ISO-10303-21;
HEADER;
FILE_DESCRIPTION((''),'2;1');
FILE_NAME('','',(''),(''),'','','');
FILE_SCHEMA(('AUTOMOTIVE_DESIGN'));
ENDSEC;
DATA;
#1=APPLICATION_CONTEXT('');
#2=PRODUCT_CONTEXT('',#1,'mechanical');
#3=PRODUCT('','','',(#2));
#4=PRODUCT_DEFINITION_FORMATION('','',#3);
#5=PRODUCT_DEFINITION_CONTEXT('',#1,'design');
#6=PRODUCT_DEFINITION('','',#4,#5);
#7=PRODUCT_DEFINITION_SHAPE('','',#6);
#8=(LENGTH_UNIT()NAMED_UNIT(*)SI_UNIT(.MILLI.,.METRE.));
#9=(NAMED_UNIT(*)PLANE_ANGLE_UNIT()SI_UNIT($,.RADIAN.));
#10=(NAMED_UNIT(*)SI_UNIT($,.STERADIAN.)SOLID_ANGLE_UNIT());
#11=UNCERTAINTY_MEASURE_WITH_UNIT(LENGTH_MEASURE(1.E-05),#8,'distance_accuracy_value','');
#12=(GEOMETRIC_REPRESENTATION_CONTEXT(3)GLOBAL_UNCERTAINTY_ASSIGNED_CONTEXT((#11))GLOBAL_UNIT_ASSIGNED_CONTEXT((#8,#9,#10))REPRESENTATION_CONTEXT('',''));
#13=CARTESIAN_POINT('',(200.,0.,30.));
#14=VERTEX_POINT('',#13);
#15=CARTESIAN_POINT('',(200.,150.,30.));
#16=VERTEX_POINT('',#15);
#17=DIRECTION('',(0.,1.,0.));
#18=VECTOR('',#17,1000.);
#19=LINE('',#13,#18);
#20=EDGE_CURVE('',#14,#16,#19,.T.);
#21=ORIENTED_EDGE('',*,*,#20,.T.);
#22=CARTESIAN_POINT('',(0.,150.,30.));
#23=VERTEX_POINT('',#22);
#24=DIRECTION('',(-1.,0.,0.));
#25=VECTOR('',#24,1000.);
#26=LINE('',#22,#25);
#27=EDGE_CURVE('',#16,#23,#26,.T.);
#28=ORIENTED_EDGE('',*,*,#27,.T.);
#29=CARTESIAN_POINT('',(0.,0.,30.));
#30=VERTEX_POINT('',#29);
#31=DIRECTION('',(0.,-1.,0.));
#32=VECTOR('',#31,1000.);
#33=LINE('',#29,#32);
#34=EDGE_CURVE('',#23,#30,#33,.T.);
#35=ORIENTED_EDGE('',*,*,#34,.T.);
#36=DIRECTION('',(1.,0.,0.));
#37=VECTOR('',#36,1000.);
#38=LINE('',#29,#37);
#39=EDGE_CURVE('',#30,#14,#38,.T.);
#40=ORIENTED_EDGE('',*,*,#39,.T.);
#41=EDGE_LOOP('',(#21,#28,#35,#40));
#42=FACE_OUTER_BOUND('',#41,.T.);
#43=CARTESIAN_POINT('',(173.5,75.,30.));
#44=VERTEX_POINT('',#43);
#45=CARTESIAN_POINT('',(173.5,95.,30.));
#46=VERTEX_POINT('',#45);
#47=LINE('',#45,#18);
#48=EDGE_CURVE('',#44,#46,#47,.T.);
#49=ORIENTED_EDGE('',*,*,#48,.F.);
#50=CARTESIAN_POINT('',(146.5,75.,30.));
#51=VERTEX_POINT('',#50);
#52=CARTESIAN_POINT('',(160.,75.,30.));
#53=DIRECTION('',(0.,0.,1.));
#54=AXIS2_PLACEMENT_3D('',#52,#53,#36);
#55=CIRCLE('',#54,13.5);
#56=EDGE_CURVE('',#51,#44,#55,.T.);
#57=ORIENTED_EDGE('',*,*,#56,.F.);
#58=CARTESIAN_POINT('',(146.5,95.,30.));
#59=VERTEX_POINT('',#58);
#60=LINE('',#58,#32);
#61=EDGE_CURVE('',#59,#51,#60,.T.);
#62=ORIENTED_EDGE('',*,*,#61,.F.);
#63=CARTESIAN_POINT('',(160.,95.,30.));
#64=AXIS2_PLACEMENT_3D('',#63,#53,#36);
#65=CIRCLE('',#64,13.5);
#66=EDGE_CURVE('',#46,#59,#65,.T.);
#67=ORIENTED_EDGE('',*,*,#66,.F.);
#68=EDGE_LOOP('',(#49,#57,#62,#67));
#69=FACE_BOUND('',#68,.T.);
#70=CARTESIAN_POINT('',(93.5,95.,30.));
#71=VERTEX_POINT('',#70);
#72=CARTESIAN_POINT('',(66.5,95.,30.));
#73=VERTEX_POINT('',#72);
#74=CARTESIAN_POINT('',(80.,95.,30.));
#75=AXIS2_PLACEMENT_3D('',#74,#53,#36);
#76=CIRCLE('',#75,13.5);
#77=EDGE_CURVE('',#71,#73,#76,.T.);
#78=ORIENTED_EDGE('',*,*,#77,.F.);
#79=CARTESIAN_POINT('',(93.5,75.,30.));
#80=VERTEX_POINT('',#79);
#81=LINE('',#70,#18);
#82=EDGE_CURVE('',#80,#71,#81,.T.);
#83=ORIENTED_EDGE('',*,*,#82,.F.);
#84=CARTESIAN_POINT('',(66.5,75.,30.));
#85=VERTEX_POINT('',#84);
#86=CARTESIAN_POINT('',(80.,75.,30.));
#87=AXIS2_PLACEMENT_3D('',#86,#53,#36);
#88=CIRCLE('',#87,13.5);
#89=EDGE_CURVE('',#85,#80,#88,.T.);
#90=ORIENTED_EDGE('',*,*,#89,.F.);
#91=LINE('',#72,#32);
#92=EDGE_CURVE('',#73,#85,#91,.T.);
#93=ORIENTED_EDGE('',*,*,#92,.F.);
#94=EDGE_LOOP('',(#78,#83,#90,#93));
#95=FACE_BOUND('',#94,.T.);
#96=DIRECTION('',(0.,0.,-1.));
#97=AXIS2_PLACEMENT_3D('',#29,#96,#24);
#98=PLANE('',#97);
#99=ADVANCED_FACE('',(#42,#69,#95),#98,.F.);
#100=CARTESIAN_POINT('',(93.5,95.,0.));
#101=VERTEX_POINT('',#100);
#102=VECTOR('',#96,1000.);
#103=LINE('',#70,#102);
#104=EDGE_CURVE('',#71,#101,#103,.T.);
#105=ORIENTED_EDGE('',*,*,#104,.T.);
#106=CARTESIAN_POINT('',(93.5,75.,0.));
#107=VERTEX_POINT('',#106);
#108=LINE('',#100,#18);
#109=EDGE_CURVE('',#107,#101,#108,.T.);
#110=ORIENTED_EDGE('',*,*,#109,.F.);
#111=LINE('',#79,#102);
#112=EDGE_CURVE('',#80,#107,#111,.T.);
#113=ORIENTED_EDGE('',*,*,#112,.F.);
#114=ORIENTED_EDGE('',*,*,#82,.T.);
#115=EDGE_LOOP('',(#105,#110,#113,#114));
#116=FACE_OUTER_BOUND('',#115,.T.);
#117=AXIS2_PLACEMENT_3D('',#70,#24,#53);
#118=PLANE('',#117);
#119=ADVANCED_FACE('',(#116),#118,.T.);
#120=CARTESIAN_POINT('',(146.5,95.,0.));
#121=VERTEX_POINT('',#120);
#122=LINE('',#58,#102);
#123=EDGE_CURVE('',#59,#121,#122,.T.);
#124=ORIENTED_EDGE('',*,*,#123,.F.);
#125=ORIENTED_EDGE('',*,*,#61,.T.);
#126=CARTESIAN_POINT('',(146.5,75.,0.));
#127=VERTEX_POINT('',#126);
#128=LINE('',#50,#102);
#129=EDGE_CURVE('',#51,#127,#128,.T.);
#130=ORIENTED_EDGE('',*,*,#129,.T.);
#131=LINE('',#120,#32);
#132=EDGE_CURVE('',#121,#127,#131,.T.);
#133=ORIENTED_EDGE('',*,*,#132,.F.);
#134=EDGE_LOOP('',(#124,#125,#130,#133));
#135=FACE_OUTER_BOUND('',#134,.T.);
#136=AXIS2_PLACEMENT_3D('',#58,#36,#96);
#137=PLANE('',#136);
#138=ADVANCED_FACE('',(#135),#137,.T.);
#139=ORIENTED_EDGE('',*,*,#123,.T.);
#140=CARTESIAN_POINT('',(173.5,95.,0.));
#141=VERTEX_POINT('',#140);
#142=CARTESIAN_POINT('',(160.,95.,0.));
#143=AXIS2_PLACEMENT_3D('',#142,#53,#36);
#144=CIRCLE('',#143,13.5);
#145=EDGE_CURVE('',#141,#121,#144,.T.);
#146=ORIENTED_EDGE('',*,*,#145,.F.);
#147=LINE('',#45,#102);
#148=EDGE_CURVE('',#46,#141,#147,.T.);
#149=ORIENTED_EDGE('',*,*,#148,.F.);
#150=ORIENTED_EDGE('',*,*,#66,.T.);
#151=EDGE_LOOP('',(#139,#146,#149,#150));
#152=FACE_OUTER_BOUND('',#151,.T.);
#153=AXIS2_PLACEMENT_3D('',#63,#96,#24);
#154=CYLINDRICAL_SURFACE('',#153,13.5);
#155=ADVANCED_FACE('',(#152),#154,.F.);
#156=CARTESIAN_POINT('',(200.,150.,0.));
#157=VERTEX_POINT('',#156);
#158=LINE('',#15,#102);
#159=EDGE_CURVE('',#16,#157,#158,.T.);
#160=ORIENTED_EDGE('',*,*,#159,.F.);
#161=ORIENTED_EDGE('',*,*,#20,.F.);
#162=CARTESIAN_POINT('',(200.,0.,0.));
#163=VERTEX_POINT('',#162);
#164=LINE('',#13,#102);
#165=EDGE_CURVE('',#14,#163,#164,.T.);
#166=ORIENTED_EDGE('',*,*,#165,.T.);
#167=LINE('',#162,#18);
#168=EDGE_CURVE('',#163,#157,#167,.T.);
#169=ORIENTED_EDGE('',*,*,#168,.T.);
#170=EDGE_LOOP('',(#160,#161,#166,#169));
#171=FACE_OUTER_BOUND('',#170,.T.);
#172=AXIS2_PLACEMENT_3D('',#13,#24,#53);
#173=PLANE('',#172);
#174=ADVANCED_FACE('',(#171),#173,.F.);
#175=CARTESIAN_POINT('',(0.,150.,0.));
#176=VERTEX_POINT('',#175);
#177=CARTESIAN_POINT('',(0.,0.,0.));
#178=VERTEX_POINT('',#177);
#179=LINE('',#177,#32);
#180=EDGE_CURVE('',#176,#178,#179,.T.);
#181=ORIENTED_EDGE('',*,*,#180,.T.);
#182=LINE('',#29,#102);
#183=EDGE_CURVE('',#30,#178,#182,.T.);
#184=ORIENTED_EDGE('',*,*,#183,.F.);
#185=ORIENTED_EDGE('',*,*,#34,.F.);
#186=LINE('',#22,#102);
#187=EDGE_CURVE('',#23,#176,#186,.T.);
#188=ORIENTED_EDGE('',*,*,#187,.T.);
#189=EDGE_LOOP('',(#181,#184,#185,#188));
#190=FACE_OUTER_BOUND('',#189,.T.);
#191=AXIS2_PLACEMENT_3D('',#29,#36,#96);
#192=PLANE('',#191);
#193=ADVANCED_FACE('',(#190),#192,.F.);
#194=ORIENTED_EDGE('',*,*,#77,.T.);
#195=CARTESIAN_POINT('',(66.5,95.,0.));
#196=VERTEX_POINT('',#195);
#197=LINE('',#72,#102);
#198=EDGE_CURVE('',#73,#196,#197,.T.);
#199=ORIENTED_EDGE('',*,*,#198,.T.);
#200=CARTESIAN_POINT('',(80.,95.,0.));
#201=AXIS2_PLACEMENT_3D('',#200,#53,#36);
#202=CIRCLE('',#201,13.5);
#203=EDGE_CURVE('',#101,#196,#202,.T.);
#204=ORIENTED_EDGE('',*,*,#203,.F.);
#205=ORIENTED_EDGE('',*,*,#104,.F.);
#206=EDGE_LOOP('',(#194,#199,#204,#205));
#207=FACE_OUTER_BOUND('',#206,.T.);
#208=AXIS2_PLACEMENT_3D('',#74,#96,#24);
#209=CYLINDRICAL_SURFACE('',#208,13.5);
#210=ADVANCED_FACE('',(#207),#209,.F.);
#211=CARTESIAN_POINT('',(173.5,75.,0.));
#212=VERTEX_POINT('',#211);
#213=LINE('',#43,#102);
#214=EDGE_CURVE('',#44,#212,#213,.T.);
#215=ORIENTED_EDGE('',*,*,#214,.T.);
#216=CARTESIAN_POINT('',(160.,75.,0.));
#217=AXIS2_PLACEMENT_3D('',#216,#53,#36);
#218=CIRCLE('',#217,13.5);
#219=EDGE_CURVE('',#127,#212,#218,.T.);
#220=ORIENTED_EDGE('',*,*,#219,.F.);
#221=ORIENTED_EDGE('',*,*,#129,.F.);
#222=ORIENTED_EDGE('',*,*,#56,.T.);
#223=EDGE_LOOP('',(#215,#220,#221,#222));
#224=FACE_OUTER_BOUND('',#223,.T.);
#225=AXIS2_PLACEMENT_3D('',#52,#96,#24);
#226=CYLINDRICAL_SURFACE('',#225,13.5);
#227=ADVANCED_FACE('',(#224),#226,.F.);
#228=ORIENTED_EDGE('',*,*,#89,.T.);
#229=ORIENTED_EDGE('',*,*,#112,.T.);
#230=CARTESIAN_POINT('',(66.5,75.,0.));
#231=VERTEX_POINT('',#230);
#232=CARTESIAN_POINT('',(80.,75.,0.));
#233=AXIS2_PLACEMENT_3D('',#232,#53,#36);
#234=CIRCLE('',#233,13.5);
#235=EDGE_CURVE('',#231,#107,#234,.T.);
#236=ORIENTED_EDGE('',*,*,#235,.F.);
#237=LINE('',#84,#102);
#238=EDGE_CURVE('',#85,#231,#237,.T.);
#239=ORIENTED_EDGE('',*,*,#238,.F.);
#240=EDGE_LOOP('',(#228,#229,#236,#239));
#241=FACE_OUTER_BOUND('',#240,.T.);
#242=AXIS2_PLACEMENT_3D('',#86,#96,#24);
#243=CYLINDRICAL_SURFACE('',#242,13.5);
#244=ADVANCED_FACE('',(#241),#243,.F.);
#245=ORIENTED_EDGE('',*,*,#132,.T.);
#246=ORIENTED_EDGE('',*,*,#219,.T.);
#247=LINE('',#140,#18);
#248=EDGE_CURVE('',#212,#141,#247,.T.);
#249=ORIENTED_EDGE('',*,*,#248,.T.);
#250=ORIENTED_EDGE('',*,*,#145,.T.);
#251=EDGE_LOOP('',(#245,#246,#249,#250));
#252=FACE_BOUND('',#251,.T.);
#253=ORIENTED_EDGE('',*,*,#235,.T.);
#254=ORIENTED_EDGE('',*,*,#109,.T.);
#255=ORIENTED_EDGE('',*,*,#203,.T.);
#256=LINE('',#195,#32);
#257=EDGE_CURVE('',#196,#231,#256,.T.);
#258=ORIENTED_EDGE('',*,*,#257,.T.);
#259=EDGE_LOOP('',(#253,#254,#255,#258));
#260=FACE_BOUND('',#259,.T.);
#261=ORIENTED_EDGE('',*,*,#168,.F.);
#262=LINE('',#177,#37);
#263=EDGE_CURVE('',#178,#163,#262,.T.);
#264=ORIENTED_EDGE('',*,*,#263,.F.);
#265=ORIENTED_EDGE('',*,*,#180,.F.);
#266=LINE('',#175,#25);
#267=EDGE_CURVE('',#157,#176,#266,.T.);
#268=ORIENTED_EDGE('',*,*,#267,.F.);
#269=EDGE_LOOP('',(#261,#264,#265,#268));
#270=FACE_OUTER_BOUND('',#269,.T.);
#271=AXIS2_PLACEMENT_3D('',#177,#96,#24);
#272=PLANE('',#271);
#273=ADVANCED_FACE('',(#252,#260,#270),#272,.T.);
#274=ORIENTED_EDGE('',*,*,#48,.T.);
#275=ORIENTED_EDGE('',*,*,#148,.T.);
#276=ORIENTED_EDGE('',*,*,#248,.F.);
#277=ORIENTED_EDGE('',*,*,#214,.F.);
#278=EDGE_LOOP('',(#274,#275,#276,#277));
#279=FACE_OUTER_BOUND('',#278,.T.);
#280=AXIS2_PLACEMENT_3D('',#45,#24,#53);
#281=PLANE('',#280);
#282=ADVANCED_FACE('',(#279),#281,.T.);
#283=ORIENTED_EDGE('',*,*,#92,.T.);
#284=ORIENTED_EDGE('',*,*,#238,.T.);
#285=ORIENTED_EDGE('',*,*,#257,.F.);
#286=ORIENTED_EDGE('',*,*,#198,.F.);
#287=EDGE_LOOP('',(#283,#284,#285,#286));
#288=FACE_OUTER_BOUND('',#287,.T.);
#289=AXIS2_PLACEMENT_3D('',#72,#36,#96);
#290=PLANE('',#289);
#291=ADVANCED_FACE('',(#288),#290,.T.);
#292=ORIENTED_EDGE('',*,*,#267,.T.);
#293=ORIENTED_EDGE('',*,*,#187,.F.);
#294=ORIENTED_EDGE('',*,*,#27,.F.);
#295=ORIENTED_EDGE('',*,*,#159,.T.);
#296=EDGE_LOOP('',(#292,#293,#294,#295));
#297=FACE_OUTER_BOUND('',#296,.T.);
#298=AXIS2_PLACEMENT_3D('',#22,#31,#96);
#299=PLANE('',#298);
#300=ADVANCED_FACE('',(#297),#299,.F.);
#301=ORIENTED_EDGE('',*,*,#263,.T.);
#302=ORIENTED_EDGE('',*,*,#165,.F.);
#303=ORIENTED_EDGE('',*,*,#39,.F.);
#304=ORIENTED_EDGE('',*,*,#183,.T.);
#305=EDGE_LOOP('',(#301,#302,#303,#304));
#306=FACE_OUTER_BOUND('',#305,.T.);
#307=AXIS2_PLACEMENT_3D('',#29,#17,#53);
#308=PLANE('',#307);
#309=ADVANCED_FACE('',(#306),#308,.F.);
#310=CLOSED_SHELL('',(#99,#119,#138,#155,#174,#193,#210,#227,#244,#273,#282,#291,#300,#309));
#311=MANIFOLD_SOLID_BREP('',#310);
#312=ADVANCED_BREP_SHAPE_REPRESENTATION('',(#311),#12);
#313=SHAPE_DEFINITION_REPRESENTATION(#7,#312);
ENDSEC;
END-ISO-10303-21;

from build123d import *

# Parameters (mm, degrees)
SKETCH1_W           = 200
SKETCH1_H           = 150
BOSS_EXTRUDE1_DEPTH = 30


with BuildPart() as part:
    # Sketch1 → Boss-Extrude1 (new body)
    with BuildSketch(Plane.XY):
        with Locations((100, 75)):
            Rectangle(SKETCH1_W, SKETCH1_H)
        with BuildLine():
            Line((93.5, 95), (93.5, 75))
            ThreePointArc((93.5, 75), (80, 61.5), (66.5, 75))
            Line((66.5, 75), (66.5, 95))
            ThreePointArc((66.5, 95), (80, 108.5), (93.5, 95))
        make_face(mode=Mode.SUBTRACT)
        with BuildLine():
            Line((173.5, 95), (173.5, 75))
            ThreePointArc((173.5, 75), (160, 61.5), (146.5, 75))
            Line((146.5, 75), (146.5, 95))
            ThreePointArc((146.5, 95), (160, 108.5), (173.5, 95))
        make_face(mode=Mode.SUBTRACT)
    extrude(amount=BOSS_EXTRUDE1_DEPTH)


solid = part.part
